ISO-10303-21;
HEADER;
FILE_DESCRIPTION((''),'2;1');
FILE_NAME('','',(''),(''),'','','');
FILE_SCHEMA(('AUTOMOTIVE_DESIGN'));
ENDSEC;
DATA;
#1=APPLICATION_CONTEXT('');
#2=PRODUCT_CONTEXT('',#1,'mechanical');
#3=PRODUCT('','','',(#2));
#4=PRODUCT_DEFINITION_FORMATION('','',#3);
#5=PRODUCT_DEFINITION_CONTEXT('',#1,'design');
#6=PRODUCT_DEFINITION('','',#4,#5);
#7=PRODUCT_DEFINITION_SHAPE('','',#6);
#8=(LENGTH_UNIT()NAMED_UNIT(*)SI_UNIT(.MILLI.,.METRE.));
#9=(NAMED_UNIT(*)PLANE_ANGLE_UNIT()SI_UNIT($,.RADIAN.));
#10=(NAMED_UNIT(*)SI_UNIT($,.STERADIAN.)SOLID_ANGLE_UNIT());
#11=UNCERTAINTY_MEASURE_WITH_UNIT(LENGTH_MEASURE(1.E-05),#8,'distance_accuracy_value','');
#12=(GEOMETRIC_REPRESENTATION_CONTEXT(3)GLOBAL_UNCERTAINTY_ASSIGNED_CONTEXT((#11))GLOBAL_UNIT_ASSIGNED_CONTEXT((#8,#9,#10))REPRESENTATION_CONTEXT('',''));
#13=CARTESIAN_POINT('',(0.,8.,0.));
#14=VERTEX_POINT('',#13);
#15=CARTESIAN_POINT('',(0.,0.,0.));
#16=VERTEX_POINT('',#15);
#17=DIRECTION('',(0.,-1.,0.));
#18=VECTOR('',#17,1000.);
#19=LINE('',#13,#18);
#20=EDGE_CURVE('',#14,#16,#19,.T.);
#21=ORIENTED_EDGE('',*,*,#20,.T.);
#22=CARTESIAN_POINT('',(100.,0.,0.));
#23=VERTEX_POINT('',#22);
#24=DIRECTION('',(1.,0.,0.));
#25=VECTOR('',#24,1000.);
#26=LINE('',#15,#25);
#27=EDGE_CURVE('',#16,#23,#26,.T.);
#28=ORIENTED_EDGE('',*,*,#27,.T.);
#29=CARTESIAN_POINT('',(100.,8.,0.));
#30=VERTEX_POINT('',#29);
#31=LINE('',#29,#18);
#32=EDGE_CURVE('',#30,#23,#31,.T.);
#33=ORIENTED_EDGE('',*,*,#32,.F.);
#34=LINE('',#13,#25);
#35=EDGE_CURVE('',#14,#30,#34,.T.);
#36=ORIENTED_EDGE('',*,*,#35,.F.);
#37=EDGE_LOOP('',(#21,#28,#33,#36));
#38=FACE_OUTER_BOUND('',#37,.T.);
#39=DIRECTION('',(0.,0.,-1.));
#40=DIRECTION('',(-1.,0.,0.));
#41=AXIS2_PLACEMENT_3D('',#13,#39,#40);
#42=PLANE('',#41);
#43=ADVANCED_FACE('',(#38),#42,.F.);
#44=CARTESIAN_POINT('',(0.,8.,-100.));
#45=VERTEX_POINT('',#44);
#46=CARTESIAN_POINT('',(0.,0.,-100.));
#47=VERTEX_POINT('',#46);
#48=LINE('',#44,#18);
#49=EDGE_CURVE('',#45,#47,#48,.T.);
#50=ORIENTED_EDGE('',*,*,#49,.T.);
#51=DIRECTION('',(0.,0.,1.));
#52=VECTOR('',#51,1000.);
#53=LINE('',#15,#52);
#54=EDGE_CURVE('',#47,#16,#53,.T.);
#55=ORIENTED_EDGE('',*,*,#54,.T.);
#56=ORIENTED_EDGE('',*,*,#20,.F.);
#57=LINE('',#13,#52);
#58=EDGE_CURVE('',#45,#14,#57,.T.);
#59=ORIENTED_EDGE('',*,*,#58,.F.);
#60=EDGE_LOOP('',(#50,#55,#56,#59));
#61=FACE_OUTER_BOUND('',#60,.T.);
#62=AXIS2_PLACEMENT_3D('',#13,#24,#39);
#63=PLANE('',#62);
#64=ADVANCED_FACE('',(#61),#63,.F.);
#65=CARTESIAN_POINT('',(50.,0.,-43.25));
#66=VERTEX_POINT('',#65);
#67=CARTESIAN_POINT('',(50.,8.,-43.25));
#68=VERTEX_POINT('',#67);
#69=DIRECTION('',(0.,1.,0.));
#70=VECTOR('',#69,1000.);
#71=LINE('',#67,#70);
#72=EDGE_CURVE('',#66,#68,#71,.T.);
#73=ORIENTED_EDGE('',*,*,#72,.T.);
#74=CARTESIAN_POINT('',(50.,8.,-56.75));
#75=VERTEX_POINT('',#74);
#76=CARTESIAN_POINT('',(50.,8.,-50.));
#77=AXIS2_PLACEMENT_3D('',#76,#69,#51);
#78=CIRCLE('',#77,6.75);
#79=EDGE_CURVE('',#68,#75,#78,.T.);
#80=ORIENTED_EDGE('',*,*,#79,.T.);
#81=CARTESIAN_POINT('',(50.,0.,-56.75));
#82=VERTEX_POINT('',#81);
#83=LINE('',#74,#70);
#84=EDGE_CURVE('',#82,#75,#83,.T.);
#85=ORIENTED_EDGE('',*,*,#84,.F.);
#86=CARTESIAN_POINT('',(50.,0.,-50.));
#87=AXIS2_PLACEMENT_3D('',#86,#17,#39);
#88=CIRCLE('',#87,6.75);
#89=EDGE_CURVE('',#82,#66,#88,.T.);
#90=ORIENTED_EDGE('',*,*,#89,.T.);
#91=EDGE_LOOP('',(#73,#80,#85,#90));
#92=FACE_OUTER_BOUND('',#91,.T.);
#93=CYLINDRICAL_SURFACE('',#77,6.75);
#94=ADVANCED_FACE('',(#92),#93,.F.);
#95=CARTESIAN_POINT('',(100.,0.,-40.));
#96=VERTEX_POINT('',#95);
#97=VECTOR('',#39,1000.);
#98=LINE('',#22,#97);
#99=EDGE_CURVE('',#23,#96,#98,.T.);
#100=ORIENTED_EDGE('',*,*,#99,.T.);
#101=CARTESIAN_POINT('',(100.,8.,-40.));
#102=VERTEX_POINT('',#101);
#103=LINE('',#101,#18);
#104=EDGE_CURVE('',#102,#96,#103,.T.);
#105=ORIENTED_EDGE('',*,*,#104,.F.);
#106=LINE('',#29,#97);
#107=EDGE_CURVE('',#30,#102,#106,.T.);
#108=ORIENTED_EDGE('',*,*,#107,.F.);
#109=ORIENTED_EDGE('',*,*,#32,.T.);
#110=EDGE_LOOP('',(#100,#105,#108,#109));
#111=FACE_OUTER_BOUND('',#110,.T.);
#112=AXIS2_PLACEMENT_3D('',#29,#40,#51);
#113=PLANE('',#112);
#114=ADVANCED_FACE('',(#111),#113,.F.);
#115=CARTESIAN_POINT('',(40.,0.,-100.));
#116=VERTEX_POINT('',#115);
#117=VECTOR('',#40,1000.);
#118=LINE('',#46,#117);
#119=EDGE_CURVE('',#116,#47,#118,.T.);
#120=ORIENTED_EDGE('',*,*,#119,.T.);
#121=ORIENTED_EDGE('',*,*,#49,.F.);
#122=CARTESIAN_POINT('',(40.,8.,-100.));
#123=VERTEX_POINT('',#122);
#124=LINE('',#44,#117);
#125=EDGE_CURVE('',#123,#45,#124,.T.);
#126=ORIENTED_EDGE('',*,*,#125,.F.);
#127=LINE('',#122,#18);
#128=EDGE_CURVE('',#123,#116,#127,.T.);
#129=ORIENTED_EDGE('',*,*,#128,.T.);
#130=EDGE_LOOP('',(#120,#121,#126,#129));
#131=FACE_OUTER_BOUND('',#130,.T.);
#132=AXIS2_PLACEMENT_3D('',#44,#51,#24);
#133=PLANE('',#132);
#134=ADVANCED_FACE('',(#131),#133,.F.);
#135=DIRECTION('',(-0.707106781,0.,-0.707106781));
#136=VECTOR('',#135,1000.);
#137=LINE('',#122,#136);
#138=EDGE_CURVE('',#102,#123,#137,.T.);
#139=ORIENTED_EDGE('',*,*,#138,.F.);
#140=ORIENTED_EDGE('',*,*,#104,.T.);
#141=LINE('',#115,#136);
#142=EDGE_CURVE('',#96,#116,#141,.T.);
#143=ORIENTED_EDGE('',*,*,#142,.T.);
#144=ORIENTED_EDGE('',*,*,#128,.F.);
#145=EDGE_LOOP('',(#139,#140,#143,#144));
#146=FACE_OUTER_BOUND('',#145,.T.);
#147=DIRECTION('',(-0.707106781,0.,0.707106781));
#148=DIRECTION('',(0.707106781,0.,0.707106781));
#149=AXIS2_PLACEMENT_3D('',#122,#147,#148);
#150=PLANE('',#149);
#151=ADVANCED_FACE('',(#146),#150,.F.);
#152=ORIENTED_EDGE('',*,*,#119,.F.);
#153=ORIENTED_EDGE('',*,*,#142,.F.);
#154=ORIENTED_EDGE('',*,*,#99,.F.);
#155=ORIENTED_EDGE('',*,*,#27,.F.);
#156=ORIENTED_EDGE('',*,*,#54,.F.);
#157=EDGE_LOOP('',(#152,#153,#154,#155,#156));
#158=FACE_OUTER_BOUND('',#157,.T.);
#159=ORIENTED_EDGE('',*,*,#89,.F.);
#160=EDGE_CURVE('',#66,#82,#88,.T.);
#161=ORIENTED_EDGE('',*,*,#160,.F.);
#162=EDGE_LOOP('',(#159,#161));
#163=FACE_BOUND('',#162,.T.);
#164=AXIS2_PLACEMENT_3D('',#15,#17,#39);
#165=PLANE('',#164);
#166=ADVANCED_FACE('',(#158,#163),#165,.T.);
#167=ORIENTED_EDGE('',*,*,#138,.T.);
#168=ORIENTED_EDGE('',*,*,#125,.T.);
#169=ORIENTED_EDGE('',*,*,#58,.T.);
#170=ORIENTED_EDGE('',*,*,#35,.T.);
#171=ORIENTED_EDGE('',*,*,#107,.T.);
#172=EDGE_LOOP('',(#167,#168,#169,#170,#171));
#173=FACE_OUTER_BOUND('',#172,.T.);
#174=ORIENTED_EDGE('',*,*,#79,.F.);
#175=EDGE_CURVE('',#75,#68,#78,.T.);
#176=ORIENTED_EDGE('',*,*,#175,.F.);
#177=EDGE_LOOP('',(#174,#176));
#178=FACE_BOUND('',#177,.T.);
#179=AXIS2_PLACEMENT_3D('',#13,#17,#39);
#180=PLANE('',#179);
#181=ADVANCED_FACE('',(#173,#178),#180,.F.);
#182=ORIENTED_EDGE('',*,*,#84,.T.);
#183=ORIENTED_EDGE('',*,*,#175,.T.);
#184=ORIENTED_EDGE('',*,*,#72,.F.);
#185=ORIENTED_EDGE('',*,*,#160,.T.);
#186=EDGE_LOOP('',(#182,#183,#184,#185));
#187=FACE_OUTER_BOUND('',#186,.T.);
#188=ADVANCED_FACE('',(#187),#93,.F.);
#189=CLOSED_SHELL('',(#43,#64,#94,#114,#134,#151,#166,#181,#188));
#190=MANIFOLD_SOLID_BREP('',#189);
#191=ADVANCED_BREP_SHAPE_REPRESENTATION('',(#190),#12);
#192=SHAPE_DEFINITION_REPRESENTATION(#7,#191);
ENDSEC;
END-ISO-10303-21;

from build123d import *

# Parameters (mm, degrees)
BOSS_EXTRUDE1_DEPTH       = 8
M12_CLEARANCE_HOLE1_D     = 13.5
M12_CLEARANCE_HOLE1_DEPTH = 60
M12_CLEARANCE_HOLE1_TIP   = 4.055809178


with BuildPart() as part:
    # Sketch1 → Boss-Extrude1 (new body)
    with BuildSketch(Plane(origin=(0, 0, 0), x_dir=(1, 0, 0), z_dir=(0, 1, 0))):
        Polygon((0, 0), (100, 0), (100, 40), (40, 100), (0, 100), align=None)
    extrude(amount=BOSS_EXTRUDE1_DEPTH)

    # M12 Clearance Hole1
    with Locations(Plane(origin=(0, 8, 0), x_dir=(1, 0, 0), z_dir=(0, 1, 0))):
        with Locations((50, 50)):
            Hole(M12_CLEARANCE_HOLE1_D / 2, depth=M12_CLEARANCE_HOLE1_DEPTH)
            with Locations((0, 0, -(M12_CLEARANCE_HOLE1_DEPTH + M12_CLEARANCE_HOLE1_TIP / 2))):  # 118° drill point
                Cone(0, M12_CLEARANCE_HOLE1_D / 2, M12_CLEARANCE_HOLE1_TIP, mode=Mode.SUBTRACT)


solid = part.part
